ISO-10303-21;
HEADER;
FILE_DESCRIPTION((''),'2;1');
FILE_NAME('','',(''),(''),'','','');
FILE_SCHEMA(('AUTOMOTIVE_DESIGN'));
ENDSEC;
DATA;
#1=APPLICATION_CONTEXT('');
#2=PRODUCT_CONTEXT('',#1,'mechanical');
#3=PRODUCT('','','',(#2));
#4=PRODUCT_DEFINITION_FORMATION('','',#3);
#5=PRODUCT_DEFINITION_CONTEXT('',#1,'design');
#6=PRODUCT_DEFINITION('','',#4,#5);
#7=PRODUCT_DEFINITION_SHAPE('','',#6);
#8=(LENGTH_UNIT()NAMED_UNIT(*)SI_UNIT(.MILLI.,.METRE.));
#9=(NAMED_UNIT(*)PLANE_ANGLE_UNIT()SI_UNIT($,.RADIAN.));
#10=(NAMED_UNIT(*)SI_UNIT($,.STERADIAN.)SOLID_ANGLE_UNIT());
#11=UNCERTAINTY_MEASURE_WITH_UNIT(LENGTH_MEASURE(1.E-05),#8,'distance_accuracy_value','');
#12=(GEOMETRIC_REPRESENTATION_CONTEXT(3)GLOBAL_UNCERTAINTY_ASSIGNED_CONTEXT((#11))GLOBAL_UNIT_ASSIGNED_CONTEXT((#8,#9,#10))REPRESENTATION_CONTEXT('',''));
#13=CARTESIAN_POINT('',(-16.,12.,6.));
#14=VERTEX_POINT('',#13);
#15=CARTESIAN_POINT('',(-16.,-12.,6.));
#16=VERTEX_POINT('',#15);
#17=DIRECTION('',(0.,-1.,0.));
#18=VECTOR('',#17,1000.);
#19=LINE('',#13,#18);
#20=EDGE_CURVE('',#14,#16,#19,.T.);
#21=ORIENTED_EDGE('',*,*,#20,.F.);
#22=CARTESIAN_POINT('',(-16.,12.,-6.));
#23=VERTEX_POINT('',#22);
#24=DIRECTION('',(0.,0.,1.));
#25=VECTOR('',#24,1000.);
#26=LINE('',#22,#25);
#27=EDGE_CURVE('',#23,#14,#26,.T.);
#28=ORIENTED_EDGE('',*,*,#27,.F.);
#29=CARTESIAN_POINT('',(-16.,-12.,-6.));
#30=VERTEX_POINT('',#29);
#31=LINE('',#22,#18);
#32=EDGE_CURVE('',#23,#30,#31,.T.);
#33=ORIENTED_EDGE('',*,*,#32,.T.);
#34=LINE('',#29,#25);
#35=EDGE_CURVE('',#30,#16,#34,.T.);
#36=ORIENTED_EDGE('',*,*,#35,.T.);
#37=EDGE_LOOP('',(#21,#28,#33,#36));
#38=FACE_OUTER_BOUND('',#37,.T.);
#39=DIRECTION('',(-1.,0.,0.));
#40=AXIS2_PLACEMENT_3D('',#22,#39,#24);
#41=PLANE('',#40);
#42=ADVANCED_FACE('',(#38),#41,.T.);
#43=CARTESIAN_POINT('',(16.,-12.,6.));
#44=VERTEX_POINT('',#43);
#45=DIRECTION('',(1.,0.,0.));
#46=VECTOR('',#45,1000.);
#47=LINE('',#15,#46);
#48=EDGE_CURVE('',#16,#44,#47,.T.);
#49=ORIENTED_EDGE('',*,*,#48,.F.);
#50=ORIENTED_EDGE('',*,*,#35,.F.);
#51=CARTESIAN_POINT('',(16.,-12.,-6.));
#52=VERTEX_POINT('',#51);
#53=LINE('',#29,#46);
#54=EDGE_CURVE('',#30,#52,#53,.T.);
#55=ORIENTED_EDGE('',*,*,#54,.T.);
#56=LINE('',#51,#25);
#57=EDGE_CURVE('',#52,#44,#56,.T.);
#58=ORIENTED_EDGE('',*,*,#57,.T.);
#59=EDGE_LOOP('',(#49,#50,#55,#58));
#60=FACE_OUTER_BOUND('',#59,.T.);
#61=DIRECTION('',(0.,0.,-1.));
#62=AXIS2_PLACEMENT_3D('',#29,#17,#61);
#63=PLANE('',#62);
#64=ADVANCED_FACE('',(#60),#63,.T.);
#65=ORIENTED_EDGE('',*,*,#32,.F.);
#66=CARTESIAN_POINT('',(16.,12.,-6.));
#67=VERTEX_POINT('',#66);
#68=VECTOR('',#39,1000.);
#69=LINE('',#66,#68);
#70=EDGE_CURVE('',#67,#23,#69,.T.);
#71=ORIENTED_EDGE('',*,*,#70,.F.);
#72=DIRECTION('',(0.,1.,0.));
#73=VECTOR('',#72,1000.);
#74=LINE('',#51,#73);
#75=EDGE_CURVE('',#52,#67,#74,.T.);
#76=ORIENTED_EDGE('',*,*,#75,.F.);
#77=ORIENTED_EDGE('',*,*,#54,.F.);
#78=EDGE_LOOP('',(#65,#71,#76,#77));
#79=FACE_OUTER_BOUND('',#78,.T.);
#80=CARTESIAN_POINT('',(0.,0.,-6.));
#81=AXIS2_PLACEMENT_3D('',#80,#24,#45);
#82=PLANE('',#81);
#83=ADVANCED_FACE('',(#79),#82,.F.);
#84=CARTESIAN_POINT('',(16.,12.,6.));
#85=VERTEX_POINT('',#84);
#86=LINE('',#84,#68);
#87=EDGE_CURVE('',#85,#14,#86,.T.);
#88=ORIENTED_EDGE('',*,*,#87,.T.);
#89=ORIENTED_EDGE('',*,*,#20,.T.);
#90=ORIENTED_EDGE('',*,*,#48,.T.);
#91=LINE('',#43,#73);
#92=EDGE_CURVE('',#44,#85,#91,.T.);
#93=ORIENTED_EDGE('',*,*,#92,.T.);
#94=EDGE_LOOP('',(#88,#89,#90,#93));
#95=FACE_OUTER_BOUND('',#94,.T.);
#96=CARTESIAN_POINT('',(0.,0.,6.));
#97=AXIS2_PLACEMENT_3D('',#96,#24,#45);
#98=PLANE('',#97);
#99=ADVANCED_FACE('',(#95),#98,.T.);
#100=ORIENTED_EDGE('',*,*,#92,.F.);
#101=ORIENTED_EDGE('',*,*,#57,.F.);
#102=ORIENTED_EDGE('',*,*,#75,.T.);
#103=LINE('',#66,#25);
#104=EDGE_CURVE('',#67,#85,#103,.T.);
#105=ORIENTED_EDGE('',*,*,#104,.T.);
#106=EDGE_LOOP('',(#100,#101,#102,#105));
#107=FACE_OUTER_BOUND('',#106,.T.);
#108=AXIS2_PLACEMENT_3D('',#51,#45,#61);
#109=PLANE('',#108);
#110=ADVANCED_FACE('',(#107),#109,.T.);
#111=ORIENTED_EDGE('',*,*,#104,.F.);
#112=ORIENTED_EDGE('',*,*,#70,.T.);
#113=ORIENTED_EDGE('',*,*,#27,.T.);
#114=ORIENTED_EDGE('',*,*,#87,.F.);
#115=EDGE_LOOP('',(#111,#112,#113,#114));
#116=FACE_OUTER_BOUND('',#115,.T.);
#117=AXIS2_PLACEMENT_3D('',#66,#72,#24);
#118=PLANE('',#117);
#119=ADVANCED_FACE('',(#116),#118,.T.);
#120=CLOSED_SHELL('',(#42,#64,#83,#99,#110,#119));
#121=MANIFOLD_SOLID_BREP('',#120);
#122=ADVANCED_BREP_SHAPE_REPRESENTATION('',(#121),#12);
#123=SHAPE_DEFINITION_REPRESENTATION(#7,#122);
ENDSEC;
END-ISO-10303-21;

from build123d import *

# Parameters (mm, degrees)
SKETCH_1_W      = 32
SKETCH_1_H      = 24
EXTRUDE_1_DEPTH = 6


with BuildPart() as part:
    # 草图1 → 凸台-拉伸1 (new, symmetric)
    with BuildSketch(Plane.XY):
        Rectangle(SKETCH_1_W, SKETCH_1_H)
    extrude(amount=EXTRUDE_1_DEPTH, both=True)


solid = part.part
